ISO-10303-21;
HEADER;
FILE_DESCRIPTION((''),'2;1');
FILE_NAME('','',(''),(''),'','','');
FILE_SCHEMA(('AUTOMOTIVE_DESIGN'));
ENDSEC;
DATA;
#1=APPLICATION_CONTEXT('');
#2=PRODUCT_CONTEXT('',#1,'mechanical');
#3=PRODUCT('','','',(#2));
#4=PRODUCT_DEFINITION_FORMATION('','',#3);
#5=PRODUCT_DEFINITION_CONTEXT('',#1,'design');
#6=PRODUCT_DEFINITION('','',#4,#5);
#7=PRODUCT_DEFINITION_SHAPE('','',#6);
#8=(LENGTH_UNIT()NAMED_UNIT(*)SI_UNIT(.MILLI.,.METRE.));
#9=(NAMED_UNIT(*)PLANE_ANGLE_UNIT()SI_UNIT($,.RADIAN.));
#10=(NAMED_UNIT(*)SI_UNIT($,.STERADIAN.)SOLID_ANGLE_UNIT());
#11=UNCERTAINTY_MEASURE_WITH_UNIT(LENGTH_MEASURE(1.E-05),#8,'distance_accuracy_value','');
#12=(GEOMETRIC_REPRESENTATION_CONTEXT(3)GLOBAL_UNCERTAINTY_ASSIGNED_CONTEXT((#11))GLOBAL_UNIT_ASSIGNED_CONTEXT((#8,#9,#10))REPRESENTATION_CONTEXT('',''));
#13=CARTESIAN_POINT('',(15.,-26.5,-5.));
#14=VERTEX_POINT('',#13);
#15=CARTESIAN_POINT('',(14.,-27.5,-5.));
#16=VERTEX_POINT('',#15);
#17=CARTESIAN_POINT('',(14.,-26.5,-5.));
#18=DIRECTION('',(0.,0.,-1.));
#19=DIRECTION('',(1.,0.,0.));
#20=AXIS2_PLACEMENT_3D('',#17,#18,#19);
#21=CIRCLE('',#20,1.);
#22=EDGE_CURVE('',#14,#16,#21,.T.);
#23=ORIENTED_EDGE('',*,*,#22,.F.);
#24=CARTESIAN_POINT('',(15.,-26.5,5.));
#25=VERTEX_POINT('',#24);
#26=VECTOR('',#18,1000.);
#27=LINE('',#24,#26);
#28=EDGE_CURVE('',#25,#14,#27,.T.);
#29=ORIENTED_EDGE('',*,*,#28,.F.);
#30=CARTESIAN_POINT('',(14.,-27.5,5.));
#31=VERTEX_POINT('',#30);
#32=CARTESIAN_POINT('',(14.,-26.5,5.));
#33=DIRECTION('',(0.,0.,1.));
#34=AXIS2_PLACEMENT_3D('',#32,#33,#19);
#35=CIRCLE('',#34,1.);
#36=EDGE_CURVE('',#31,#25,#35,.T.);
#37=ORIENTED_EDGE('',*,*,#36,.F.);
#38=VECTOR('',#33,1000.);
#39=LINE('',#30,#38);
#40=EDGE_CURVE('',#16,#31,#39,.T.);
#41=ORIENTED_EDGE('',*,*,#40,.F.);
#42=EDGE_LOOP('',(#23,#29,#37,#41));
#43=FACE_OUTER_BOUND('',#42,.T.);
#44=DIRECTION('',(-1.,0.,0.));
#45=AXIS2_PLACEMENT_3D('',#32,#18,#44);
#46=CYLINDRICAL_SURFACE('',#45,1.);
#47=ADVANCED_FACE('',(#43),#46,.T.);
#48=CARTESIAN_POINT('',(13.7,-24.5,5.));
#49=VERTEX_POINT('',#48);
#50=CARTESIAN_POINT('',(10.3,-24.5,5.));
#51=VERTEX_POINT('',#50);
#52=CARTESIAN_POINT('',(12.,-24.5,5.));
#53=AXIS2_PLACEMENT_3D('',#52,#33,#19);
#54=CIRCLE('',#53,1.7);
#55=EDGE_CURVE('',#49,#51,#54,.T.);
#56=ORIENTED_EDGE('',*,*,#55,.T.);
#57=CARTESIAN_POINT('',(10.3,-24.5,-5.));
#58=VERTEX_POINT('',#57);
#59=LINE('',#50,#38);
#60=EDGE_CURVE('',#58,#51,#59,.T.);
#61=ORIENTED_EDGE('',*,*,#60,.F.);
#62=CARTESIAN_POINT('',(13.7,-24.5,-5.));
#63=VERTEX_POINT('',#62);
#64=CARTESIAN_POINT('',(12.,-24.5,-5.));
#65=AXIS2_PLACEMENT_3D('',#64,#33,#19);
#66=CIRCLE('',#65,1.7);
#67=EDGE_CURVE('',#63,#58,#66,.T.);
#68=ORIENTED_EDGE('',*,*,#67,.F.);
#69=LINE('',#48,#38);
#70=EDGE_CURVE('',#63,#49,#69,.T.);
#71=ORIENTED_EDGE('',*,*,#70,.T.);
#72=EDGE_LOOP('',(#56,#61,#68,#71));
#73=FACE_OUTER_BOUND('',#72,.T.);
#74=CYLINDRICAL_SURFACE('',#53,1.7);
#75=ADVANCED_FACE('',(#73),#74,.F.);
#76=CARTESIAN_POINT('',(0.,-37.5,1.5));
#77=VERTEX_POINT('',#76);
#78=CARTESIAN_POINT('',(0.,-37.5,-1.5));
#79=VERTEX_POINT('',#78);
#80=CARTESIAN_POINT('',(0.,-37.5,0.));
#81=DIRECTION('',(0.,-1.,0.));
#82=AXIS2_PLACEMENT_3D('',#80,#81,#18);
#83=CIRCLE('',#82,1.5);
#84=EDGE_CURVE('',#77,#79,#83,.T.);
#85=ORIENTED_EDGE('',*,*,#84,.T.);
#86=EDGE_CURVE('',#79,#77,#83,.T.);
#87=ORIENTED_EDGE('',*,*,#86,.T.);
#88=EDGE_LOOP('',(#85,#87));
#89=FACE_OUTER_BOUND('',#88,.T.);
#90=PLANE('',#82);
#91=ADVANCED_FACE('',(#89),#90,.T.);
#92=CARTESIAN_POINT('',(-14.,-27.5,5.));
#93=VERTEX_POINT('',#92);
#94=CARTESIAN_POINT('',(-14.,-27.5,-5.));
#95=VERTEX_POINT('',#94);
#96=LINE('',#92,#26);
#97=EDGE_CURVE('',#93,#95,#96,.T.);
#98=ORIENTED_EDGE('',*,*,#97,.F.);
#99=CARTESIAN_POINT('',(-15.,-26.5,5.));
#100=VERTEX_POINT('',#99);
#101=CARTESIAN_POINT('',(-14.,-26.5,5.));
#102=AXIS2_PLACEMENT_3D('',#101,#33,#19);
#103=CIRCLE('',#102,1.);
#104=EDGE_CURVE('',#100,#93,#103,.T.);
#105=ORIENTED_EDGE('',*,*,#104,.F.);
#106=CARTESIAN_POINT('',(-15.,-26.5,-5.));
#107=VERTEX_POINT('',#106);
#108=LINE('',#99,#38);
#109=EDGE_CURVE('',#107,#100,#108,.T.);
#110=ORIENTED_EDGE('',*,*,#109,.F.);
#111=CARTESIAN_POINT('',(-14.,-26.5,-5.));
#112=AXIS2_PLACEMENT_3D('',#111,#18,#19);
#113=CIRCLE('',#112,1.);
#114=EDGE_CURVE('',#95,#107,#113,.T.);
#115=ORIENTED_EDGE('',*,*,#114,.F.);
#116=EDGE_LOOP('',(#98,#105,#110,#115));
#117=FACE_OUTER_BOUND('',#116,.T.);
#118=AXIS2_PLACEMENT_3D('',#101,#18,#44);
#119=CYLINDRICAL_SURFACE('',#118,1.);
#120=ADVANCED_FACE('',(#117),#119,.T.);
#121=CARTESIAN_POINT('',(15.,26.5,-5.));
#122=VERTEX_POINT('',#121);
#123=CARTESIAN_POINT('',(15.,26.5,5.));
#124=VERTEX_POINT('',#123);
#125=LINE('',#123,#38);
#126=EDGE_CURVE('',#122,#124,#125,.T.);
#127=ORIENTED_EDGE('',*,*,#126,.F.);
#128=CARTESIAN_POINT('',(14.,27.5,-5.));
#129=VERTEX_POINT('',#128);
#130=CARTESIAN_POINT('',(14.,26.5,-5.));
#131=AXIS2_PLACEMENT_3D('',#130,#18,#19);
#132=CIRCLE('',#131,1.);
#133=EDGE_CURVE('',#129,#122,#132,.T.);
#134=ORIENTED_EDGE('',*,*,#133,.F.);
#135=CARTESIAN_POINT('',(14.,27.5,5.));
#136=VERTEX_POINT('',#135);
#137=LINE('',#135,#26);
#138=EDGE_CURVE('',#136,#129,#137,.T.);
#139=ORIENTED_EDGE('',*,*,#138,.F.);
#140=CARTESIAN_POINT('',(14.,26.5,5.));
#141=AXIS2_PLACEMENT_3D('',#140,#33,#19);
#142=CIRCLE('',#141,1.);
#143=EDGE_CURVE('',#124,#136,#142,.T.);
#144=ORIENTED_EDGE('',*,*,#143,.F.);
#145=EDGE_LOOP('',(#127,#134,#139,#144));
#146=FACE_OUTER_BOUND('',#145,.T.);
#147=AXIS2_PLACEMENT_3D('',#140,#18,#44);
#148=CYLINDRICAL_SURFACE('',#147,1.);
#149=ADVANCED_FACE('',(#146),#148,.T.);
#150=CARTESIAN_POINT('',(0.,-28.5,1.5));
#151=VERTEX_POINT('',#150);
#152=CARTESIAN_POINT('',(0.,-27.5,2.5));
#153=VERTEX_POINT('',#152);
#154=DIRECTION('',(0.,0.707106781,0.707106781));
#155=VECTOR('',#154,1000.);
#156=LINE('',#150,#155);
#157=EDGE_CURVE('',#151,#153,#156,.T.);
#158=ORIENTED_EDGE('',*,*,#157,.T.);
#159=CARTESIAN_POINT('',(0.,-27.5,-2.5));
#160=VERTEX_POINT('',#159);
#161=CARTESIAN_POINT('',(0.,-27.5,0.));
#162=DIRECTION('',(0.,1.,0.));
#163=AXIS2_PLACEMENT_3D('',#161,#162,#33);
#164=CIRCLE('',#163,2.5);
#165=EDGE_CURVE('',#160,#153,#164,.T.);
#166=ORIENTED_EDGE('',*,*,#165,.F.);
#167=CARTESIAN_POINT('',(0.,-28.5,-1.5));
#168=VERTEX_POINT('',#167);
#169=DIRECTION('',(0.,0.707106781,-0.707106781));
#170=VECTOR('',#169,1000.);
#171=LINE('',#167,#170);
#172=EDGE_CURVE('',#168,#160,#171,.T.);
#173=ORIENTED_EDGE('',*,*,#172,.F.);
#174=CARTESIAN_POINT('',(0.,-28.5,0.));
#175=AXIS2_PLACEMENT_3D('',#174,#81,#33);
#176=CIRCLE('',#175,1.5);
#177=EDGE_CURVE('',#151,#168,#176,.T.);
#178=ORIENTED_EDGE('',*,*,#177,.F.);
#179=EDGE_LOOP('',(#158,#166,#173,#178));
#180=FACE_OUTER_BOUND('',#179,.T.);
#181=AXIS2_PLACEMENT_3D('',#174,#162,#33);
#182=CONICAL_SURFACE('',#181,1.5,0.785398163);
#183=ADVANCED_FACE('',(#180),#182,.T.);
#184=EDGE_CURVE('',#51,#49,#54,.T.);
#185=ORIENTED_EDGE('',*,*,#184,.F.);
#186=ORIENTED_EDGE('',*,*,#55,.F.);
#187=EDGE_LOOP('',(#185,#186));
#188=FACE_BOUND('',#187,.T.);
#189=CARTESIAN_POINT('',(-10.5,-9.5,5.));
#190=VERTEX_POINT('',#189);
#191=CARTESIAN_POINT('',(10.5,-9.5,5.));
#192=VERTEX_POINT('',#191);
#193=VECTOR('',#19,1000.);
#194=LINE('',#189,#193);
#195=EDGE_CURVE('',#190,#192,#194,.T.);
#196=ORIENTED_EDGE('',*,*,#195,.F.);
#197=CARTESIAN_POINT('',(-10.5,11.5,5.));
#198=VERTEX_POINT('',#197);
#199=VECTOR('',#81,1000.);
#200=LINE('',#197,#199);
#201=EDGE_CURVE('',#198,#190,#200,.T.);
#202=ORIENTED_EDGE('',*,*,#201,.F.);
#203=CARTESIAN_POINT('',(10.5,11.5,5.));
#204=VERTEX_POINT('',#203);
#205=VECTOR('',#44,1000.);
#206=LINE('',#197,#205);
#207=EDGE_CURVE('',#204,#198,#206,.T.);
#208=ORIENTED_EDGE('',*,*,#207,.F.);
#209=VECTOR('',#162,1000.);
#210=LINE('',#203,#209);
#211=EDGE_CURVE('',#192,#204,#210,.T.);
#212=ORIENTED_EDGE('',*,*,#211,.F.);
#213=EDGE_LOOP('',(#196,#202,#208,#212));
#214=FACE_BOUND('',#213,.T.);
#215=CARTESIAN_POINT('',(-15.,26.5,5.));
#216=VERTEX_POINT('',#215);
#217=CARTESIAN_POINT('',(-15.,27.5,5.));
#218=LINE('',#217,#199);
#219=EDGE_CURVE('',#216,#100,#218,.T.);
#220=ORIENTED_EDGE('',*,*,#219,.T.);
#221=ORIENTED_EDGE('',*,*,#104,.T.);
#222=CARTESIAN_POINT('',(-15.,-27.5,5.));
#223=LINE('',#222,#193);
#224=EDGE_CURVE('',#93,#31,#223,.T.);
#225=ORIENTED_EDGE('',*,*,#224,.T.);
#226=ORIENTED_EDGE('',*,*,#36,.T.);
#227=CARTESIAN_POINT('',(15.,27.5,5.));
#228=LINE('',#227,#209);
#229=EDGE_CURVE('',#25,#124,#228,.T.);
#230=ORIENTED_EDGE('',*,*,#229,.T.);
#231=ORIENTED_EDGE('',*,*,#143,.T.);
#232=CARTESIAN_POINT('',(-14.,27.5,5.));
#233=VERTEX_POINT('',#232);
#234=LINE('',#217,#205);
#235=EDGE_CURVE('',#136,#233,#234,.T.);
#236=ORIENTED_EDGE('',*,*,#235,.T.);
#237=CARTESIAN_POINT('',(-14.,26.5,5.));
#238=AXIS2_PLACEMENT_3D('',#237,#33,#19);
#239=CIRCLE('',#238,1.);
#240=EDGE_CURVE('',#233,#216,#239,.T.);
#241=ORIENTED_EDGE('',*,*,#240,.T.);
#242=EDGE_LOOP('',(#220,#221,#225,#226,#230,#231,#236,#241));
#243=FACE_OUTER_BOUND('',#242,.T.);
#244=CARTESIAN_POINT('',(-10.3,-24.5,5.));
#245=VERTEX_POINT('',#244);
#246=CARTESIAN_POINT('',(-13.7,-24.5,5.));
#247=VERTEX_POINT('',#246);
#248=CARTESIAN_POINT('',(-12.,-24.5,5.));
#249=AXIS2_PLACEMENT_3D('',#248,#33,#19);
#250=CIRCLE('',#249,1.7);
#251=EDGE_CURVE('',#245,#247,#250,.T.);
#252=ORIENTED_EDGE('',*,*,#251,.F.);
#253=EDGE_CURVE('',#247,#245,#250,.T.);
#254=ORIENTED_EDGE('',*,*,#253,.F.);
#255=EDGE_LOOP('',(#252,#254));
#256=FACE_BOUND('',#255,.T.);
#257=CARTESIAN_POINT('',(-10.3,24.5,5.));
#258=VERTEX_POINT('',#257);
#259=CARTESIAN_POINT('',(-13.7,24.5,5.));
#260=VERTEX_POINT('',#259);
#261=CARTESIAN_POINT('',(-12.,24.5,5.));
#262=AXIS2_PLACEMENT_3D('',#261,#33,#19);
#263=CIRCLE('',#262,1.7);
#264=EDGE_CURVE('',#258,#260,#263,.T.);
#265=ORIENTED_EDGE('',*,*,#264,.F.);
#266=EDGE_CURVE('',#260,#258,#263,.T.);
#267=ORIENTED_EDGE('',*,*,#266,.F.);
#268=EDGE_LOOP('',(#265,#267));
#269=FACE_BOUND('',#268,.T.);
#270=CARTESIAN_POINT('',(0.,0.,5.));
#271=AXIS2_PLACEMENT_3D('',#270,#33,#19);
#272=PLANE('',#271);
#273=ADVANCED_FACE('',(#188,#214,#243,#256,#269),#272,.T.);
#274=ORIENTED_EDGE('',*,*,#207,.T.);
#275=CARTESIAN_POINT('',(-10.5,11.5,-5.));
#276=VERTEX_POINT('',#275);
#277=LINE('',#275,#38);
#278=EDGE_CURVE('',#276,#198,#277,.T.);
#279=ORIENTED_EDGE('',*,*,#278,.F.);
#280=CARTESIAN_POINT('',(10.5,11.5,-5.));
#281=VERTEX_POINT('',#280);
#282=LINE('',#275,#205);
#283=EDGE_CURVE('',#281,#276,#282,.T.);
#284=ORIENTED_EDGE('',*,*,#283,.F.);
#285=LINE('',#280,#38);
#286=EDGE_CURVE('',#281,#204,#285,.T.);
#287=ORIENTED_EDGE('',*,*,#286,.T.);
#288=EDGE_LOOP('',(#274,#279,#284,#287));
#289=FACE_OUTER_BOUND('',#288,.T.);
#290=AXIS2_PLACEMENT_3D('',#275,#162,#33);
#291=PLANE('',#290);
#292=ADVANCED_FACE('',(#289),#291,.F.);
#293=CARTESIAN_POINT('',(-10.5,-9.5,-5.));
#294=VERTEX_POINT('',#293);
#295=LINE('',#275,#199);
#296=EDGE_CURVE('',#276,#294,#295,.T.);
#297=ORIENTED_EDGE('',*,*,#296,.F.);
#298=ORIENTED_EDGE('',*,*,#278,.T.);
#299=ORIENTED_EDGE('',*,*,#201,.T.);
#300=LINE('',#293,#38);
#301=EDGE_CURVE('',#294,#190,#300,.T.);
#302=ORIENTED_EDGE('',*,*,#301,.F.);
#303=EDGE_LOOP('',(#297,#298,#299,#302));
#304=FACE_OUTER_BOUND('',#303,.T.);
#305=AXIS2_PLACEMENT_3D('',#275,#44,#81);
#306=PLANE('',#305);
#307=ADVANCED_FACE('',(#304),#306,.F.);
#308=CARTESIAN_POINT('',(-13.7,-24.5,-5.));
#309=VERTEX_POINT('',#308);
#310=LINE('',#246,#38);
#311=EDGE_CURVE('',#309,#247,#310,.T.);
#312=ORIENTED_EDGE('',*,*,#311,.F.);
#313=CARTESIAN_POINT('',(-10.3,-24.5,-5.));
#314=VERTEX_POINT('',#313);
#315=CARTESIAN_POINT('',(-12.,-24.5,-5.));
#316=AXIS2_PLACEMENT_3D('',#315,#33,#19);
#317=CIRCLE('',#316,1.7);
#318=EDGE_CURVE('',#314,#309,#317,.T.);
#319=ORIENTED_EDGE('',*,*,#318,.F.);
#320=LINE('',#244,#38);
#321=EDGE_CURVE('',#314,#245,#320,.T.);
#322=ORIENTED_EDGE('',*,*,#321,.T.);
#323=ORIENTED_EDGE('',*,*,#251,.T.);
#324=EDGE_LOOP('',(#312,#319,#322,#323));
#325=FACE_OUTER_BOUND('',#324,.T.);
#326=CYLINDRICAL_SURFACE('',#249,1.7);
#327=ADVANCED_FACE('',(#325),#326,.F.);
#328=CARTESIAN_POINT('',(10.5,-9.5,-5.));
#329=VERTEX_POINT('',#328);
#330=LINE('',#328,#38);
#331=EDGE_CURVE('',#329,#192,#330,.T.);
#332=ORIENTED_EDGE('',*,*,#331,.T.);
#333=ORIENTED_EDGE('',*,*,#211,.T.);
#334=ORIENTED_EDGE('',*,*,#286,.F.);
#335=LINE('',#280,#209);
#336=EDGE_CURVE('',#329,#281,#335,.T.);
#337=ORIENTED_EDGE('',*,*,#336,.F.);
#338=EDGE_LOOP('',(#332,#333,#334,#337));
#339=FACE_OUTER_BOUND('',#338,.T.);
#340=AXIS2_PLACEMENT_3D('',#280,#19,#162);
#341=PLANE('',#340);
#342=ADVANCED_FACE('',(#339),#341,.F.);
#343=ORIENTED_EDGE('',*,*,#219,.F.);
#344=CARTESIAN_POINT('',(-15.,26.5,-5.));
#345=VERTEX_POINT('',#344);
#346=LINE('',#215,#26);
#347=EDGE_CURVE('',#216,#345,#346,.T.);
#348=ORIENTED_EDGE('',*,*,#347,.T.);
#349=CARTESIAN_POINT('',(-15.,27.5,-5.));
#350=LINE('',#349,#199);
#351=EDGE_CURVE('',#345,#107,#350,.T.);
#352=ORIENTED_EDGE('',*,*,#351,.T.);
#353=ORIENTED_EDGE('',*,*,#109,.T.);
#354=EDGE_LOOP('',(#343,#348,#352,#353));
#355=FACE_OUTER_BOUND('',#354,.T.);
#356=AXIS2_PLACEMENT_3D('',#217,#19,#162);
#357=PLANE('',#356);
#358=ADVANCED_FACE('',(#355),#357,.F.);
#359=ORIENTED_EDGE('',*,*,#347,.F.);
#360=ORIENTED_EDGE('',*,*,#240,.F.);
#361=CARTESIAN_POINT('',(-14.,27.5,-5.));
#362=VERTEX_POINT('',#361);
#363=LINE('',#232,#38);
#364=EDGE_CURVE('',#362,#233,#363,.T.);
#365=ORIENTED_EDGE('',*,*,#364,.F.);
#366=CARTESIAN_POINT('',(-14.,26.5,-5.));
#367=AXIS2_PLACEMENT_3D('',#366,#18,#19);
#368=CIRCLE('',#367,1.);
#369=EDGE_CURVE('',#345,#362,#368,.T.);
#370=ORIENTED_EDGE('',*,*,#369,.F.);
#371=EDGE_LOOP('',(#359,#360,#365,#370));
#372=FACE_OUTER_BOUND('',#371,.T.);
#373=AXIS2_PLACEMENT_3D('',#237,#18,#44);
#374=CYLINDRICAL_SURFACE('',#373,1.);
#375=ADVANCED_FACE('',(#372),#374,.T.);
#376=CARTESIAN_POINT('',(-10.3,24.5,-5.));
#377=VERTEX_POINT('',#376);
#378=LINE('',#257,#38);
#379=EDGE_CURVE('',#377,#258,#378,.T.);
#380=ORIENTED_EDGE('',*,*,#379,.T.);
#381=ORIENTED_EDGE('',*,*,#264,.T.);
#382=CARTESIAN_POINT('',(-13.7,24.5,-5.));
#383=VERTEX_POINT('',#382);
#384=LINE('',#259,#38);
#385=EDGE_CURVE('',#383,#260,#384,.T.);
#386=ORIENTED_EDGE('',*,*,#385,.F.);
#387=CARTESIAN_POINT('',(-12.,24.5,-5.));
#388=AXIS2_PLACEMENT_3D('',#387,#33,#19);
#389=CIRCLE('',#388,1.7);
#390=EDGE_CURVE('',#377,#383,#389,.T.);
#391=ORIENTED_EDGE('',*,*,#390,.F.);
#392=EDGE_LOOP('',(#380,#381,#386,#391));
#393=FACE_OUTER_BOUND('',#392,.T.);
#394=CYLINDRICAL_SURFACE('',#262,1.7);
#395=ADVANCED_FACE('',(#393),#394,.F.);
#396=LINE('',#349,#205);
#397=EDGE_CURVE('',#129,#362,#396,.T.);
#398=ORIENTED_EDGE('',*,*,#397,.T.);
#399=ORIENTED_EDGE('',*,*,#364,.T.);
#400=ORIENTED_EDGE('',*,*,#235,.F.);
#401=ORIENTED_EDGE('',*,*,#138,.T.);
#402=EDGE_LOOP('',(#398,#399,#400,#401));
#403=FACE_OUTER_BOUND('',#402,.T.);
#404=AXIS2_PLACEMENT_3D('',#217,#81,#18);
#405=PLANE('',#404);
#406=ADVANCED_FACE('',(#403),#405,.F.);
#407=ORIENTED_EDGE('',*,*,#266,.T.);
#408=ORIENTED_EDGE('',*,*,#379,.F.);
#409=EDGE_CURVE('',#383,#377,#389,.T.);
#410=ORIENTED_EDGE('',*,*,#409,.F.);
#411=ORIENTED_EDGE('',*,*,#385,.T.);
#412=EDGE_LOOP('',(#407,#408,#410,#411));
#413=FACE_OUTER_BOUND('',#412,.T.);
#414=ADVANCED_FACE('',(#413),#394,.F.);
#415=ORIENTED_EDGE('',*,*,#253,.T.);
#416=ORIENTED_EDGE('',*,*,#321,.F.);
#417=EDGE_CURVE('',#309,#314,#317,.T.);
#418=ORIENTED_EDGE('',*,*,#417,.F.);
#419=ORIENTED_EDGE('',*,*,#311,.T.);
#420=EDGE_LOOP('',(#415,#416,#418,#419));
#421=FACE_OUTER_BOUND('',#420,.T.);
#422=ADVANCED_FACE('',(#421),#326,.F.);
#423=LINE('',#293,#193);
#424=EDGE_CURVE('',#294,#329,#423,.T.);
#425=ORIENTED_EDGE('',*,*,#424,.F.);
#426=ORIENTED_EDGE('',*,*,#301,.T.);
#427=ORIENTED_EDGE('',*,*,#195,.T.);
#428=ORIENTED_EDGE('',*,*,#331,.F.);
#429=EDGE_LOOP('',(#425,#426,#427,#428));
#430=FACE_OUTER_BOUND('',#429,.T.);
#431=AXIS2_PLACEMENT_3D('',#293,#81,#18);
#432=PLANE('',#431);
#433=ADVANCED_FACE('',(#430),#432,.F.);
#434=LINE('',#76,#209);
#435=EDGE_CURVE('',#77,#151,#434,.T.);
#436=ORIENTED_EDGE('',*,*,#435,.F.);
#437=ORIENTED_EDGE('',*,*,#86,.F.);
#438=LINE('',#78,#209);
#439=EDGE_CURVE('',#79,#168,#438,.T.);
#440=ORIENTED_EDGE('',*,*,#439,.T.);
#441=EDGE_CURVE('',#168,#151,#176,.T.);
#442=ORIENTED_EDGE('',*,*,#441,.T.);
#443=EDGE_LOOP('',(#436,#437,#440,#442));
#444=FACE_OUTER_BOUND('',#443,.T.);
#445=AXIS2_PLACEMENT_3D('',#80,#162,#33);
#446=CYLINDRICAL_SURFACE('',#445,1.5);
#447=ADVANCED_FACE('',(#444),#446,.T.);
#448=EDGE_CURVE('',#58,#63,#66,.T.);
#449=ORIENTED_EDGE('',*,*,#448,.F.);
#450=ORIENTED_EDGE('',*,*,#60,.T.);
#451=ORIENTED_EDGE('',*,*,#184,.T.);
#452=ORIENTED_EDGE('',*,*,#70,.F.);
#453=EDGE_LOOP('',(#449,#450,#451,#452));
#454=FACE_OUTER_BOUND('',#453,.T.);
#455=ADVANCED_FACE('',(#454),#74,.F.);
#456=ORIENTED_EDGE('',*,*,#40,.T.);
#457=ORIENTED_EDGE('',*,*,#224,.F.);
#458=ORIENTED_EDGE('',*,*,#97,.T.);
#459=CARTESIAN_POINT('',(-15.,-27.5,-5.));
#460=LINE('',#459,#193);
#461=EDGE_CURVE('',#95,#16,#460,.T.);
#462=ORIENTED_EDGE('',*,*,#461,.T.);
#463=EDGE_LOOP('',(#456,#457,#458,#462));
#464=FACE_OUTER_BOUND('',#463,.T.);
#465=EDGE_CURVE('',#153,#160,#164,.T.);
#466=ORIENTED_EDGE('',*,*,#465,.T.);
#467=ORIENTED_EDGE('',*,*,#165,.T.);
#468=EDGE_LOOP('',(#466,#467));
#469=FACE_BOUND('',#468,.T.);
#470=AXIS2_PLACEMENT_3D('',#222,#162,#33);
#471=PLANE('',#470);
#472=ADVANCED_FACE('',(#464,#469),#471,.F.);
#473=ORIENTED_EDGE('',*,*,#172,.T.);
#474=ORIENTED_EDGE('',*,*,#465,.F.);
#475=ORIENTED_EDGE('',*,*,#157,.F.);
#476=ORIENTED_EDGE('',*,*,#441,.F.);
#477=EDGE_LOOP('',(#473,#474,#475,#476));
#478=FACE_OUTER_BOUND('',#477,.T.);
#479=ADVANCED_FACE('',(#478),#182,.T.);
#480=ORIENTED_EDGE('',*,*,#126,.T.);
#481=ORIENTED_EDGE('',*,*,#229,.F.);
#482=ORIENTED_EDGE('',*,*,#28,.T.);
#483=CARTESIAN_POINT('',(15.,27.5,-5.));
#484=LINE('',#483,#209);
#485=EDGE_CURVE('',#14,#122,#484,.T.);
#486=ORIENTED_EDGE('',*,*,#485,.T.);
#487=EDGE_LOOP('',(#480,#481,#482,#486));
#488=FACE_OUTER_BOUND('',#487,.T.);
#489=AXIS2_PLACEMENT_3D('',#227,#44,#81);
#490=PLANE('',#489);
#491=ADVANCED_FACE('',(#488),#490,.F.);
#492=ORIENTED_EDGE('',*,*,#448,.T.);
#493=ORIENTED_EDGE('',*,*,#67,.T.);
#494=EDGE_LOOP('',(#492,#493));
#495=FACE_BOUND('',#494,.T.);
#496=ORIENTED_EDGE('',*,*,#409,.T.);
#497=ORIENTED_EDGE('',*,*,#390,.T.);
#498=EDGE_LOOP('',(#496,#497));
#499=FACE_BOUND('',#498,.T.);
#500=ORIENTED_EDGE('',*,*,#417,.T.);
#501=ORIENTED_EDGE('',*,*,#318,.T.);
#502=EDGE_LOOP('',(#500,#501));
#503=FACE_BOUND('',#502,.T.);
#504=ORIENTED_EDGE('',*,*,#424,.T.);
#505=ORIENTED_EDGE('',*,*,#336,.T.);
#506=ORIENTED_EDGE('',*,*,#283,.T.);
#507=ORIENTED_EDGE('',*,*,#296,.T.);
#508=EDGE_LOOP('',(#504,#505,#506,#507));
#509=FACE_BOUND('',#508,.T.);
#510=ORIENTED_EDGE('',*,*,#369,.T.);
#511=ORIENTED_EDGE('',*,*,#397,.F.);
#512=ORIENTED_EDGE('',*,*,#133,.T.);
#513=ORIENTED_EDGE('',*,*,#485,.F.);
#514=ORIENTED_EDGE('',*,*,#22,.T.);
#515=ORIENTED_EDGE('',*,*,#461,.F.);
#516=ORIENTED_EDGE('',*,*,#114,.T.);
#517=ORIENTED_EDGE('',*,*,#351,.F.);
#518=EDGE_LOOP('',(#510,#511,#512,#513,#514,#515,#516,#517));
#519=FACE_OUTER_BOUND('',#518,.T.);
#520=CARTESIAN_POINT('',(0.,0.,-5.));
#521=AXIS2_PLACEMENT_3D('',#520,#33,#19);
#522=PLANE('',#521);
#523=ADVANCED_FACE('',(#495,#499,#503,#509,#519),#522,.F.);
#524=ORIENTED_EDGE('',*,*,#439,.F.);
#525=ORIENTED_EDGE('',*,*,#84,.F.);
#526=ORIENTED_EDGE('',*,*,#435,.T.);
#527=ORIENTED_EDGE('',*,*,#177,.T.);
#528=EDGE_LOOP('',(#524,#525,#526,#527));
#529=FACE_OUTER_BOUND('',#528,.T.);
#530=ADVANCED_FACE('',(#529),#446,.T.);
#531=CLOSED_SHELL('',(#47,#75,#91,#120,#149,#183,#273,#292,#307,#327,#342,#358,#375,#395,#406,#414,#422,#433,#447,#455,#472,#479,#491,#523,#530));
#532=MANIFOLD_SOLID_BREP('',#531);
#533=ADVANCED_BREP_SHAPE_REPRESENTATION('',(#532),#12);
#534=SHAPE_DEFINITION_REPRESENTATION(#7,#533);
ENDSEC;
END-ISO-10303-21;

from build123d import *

# Parameters (mm, degrees)
SKETCH1_W                  = 30
SKETCH1_H                  = 55
BOSS_EXTRUDE1_DEPTH        = 5
SKETCH2_W                  = 21
SKETCH2_H                  = 21
CUT_EXTRUDE1_DEPTH         = 33.882366095
SKETCH3_R                  = 1.5
BOSS_EXTRUDE2_DEPTH        = 10
CHAMFER1_SIZE              = 1
FILLET1_R                  = 1
F_3_4_3_4_DIAMETER_HOLE1_D = 3.4


with BuildPart() as part:
    # Sketch1 → Boss-Extrude1 (new, symmetric)
    with BuildSketch(Plane.XY):
        Rectangle(SKETCH1_W, SKETCH1_H)
    extrude(amount=BOSS_EXTRUDE1_DEPTH, both=True)

    # Sketch2 → Cut-Extrude1 (cut, through all)
    with BuildSketch(Plane.XY.offset(5)):
        with Locations((0, 1)):
            Rectangle(SKETCH2_W, SKETCH2_H)
    extrude(amount=-CUT_EXTRUDE1_DEPTH, mode=Mode.SUBTRACT)

    # Sketch3 → Boss-Extrude2 (add)
    with BuildSketch(Plane.XZ.offset(27.5)):
        with Locations(Location((0, 0, 0), (0, 0, 90))):
            Circle(SKETCH3_R)
    extrude(amount=BOSS_EXTRUDE2_DEPTH)

    # Chamfer1
    chamfer1_edges = [part.edges().sort_by_distance(p)[0] for p in [
        (0, -27.5, -1.5),
    ]]
    chamfer(chamfer1_edges, length=CHAMFER1_SIZE)

    # Fillet1
    fillet1_edges = [part.edges().sort_by_distance(p)[0] for p in [
        (15, -27.5, 0),
        (-15, -27.5, 0),
        (-15, 27.5, 0),
        (15, 27.5, 0),
    ]]
    fillet(fillet1_edges, radius=FILLET1_R)

    # Ø3.4 (3.4) Diameter Hole1 (through all)
    with Locations(Plane.XY.offset(5)):
        with Locations((-12, 24.5), (-12, -24.5), (12, -24.5)):
            Hole(F_3_4_3_4_DIAMETER_HOLE1_D / 2)


solid = part.part
